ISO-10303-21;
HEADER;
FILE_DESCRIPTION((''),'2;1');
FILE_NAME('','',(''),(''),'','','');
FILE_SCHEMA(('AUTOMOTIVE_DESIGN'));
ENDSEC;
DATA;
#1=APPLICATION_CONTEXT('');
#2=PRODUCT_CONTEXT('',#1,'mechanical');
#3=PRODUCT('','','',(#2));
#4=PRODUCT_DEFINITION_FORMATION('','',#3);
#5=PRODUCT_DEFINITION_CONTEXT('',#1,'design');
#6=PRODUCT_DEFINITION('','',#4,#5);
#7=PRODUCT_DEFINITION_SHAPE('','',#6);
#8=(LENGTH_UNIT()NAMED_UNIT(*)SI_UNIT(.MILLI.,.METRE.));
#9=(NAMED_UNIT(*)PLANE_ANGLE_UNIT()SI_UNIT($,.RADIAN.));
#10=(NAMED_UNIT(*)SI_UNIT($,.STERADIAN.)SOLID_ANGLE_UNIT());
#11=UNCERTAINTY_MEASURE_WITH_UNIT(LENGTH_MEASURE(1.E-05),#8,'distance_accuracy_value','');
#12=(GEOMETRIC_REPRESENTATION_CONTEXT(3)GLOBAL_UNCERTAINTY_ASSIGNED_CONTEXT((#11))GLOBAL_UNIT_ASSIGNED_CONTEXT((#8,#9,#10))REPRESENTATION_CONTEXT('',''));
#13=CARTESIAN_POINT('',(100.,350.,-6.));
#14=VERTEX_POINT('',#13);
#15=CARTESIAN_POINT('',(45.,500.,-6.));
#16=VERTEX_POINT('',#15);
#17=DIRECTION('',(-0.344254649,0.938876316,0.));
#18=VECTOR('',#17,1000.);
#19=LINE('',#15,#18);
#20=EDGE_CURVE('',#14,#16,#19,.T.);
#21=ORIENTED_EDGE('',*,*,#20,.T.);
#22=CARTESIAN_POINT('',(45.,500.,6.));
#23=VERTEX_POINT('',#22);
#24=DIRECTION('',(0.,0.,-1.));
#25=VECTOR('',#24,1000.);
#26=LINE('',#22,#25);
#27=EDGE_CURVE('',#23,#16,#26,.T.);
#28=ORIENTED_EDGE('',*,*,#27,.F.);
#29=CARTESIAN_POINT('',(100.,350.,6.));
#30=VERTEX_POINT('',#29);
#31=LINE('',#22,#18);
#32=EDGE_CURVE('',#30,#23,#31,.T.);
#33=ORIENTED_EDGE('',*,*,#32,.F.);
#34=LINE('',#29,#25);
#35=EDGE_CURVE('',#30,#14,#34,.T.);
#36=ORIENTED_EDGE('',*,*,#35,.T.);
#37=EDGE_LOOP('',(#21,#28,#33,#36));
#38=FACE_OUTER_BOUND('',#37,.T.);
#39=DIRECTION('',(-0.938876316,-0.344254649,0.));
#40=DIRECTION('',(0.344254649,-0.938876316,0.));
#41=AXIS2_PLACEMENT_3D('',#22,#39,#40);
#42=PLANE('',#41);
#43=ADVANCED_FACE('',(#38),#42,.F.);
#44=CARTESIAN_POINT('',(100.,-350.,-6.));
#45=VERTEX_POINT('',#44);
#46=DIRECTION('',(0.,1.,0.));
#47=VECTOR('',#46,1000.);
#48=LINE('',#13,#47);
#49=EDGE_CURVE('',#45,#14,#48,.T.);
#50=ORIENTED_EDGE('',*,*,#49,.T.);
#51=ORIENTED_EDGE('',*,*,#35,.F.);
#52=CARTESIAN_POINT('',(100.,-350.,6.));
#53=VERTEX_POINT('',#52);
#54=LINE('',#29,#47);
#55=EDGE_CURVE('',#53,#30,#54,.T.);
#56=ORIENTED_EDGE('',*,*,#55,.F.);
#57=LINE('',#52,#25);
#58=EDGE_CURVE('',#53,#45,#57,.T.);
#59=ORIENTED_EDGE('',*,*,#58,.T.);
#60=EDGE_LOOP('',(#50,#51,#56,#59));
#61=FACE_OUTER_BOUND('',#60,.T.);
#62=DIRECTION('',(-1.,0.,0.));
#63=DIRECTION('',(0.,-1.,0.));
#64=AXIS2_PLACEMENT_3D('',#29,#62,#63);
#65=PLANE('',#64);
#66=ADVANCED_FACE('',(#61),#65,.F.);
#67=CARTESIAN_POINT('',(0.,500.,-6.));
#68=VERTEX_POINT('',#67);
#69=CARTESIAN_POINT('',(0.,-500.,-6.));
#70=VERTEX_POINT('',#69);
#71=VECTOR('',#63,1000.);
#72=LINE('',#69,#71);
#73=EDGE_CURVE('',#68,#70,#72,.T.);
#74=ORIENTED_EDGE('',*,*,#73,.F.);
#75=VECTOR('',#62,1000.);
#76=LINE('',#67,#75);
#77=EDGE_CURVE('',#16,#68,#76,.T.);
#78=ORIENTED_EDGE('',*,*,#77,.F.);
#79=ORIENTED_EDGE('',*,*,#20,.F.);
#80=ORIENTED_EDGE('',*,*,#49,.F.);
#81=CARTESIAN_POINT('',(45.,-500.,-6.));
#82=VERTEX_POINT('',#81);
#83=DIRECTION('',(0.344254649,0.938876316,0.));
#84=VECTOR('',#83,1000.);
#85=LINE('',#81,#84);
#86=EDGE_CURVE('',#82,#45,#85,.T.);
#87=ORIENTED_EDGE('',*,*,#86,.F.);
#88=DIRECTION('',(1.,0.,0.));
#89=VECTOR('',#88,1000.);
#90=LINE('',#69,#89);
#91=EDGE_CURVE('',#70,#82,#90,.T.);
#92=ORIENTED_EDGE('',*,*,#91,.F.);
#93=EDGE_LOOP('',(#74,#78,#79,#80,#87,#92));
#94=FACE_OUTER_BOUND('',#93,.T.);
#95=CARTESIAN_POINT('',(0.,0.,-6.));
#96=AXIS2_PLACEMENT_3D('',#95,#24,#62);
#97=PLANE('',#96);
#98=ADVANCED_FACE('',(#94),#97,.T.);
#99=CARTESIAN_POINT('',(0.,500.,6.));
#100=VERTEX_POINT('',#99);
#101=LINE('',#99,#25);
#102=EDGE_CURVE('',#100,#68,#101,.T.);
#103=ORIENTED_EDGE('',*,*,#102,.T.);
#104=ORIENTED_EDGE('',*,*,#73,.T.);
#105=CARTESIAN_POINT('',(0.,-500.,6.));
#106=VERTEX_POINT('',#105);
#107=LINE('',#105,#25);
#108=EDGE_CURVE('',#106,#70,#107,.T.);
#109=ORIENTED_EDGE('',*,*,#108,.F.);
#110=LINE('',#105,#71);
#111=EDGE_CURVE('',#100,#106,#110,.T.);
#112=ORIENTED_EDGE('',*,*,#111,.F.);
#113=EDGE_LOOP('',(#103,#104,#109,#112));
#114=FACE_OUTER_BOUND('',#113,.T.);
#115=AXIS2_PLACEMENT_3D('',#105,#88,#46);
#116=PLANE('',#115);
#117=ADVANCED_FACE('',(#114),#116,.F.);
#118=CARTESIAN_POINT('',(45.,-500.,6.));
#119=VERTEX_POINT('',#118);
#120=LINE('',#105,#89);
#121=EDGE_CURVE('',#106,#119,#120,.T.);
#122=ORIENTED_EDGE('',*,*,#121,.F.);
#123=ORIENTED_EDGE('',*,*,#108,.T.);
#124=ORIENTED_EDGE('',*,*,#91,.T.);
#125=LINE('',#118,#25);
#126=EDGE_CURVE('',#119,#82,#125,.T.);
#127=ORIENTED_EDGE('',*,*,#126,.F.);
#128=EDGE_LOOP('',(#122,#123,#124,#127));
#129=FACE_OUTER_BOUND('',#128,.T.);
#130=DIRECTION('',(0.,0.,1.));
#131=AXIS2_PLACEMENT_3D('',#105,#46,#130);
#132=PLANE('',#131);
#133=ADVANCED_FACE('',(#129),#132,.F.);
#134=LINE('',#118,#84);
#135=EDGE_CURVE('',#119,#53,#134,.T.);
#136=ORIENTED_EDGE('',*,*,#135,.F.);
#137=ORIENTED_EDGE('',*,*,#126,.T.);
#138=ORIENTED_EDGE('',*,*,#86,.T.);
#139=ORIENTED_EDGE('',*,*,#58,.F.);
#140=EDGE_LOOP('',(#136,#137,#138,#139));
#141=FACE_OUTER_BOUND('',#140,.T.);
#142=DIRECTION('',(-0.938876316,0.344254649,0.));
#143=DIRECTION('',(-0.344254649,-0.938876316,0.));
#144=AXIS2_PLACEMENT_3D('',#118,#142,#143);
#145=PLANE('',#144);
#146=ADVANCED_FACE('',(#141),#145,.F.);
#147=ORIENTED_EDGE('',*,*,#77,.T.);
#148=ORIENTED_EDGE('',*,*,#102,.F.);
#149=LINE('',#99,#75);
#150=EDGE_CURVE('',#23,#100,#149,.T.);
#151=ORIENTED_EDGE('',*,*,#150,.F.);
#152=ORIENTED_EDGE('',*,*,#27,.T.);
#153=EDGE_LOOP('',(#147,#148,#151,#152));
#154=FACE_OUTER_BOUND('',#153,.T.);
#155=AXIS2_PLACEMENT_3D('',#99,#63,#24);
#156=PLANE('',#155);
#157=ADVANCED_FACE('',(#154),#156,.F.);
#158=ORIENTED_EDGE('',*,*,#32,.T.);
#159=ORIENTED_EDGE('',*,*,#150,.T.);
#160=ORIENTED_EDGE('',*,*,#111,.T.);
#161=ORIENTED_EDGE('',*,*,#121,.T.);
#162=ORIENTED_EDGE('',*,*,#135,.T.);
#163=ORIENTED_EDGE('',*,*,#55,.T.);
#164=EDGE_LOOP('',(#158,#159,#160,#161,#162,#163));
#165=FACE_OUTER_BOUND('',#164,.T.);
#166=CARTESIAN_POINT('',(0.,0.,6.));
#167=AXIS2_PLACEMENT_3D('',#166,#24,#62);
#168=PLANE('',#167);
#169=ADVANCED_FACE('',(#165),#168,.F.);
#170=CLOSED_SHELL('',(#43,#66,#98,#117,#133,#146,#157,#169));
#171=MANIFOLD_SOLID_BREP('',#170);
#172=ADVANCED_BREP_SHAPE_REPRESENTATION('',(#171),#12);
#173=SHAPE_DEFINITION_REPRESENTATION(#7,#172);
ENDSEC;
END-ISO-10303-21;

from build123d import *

# Parameters (mm, degrees)
BOSS_EXTRUDE1_DEPTH = 6


with BuildPart() as part:
    # Sketch1 → Boss-Extrude1 (new, symmetric)
    with BuildSketch(Plane.XY):
        Polygon((0, -500), (0, 500), (45, 500), (100, 350), (100, -350), (45, -500), align=None)
    extrude(amount=BOSS_EXTRUDE1_DEPTH, both=True)


solid = part.part
